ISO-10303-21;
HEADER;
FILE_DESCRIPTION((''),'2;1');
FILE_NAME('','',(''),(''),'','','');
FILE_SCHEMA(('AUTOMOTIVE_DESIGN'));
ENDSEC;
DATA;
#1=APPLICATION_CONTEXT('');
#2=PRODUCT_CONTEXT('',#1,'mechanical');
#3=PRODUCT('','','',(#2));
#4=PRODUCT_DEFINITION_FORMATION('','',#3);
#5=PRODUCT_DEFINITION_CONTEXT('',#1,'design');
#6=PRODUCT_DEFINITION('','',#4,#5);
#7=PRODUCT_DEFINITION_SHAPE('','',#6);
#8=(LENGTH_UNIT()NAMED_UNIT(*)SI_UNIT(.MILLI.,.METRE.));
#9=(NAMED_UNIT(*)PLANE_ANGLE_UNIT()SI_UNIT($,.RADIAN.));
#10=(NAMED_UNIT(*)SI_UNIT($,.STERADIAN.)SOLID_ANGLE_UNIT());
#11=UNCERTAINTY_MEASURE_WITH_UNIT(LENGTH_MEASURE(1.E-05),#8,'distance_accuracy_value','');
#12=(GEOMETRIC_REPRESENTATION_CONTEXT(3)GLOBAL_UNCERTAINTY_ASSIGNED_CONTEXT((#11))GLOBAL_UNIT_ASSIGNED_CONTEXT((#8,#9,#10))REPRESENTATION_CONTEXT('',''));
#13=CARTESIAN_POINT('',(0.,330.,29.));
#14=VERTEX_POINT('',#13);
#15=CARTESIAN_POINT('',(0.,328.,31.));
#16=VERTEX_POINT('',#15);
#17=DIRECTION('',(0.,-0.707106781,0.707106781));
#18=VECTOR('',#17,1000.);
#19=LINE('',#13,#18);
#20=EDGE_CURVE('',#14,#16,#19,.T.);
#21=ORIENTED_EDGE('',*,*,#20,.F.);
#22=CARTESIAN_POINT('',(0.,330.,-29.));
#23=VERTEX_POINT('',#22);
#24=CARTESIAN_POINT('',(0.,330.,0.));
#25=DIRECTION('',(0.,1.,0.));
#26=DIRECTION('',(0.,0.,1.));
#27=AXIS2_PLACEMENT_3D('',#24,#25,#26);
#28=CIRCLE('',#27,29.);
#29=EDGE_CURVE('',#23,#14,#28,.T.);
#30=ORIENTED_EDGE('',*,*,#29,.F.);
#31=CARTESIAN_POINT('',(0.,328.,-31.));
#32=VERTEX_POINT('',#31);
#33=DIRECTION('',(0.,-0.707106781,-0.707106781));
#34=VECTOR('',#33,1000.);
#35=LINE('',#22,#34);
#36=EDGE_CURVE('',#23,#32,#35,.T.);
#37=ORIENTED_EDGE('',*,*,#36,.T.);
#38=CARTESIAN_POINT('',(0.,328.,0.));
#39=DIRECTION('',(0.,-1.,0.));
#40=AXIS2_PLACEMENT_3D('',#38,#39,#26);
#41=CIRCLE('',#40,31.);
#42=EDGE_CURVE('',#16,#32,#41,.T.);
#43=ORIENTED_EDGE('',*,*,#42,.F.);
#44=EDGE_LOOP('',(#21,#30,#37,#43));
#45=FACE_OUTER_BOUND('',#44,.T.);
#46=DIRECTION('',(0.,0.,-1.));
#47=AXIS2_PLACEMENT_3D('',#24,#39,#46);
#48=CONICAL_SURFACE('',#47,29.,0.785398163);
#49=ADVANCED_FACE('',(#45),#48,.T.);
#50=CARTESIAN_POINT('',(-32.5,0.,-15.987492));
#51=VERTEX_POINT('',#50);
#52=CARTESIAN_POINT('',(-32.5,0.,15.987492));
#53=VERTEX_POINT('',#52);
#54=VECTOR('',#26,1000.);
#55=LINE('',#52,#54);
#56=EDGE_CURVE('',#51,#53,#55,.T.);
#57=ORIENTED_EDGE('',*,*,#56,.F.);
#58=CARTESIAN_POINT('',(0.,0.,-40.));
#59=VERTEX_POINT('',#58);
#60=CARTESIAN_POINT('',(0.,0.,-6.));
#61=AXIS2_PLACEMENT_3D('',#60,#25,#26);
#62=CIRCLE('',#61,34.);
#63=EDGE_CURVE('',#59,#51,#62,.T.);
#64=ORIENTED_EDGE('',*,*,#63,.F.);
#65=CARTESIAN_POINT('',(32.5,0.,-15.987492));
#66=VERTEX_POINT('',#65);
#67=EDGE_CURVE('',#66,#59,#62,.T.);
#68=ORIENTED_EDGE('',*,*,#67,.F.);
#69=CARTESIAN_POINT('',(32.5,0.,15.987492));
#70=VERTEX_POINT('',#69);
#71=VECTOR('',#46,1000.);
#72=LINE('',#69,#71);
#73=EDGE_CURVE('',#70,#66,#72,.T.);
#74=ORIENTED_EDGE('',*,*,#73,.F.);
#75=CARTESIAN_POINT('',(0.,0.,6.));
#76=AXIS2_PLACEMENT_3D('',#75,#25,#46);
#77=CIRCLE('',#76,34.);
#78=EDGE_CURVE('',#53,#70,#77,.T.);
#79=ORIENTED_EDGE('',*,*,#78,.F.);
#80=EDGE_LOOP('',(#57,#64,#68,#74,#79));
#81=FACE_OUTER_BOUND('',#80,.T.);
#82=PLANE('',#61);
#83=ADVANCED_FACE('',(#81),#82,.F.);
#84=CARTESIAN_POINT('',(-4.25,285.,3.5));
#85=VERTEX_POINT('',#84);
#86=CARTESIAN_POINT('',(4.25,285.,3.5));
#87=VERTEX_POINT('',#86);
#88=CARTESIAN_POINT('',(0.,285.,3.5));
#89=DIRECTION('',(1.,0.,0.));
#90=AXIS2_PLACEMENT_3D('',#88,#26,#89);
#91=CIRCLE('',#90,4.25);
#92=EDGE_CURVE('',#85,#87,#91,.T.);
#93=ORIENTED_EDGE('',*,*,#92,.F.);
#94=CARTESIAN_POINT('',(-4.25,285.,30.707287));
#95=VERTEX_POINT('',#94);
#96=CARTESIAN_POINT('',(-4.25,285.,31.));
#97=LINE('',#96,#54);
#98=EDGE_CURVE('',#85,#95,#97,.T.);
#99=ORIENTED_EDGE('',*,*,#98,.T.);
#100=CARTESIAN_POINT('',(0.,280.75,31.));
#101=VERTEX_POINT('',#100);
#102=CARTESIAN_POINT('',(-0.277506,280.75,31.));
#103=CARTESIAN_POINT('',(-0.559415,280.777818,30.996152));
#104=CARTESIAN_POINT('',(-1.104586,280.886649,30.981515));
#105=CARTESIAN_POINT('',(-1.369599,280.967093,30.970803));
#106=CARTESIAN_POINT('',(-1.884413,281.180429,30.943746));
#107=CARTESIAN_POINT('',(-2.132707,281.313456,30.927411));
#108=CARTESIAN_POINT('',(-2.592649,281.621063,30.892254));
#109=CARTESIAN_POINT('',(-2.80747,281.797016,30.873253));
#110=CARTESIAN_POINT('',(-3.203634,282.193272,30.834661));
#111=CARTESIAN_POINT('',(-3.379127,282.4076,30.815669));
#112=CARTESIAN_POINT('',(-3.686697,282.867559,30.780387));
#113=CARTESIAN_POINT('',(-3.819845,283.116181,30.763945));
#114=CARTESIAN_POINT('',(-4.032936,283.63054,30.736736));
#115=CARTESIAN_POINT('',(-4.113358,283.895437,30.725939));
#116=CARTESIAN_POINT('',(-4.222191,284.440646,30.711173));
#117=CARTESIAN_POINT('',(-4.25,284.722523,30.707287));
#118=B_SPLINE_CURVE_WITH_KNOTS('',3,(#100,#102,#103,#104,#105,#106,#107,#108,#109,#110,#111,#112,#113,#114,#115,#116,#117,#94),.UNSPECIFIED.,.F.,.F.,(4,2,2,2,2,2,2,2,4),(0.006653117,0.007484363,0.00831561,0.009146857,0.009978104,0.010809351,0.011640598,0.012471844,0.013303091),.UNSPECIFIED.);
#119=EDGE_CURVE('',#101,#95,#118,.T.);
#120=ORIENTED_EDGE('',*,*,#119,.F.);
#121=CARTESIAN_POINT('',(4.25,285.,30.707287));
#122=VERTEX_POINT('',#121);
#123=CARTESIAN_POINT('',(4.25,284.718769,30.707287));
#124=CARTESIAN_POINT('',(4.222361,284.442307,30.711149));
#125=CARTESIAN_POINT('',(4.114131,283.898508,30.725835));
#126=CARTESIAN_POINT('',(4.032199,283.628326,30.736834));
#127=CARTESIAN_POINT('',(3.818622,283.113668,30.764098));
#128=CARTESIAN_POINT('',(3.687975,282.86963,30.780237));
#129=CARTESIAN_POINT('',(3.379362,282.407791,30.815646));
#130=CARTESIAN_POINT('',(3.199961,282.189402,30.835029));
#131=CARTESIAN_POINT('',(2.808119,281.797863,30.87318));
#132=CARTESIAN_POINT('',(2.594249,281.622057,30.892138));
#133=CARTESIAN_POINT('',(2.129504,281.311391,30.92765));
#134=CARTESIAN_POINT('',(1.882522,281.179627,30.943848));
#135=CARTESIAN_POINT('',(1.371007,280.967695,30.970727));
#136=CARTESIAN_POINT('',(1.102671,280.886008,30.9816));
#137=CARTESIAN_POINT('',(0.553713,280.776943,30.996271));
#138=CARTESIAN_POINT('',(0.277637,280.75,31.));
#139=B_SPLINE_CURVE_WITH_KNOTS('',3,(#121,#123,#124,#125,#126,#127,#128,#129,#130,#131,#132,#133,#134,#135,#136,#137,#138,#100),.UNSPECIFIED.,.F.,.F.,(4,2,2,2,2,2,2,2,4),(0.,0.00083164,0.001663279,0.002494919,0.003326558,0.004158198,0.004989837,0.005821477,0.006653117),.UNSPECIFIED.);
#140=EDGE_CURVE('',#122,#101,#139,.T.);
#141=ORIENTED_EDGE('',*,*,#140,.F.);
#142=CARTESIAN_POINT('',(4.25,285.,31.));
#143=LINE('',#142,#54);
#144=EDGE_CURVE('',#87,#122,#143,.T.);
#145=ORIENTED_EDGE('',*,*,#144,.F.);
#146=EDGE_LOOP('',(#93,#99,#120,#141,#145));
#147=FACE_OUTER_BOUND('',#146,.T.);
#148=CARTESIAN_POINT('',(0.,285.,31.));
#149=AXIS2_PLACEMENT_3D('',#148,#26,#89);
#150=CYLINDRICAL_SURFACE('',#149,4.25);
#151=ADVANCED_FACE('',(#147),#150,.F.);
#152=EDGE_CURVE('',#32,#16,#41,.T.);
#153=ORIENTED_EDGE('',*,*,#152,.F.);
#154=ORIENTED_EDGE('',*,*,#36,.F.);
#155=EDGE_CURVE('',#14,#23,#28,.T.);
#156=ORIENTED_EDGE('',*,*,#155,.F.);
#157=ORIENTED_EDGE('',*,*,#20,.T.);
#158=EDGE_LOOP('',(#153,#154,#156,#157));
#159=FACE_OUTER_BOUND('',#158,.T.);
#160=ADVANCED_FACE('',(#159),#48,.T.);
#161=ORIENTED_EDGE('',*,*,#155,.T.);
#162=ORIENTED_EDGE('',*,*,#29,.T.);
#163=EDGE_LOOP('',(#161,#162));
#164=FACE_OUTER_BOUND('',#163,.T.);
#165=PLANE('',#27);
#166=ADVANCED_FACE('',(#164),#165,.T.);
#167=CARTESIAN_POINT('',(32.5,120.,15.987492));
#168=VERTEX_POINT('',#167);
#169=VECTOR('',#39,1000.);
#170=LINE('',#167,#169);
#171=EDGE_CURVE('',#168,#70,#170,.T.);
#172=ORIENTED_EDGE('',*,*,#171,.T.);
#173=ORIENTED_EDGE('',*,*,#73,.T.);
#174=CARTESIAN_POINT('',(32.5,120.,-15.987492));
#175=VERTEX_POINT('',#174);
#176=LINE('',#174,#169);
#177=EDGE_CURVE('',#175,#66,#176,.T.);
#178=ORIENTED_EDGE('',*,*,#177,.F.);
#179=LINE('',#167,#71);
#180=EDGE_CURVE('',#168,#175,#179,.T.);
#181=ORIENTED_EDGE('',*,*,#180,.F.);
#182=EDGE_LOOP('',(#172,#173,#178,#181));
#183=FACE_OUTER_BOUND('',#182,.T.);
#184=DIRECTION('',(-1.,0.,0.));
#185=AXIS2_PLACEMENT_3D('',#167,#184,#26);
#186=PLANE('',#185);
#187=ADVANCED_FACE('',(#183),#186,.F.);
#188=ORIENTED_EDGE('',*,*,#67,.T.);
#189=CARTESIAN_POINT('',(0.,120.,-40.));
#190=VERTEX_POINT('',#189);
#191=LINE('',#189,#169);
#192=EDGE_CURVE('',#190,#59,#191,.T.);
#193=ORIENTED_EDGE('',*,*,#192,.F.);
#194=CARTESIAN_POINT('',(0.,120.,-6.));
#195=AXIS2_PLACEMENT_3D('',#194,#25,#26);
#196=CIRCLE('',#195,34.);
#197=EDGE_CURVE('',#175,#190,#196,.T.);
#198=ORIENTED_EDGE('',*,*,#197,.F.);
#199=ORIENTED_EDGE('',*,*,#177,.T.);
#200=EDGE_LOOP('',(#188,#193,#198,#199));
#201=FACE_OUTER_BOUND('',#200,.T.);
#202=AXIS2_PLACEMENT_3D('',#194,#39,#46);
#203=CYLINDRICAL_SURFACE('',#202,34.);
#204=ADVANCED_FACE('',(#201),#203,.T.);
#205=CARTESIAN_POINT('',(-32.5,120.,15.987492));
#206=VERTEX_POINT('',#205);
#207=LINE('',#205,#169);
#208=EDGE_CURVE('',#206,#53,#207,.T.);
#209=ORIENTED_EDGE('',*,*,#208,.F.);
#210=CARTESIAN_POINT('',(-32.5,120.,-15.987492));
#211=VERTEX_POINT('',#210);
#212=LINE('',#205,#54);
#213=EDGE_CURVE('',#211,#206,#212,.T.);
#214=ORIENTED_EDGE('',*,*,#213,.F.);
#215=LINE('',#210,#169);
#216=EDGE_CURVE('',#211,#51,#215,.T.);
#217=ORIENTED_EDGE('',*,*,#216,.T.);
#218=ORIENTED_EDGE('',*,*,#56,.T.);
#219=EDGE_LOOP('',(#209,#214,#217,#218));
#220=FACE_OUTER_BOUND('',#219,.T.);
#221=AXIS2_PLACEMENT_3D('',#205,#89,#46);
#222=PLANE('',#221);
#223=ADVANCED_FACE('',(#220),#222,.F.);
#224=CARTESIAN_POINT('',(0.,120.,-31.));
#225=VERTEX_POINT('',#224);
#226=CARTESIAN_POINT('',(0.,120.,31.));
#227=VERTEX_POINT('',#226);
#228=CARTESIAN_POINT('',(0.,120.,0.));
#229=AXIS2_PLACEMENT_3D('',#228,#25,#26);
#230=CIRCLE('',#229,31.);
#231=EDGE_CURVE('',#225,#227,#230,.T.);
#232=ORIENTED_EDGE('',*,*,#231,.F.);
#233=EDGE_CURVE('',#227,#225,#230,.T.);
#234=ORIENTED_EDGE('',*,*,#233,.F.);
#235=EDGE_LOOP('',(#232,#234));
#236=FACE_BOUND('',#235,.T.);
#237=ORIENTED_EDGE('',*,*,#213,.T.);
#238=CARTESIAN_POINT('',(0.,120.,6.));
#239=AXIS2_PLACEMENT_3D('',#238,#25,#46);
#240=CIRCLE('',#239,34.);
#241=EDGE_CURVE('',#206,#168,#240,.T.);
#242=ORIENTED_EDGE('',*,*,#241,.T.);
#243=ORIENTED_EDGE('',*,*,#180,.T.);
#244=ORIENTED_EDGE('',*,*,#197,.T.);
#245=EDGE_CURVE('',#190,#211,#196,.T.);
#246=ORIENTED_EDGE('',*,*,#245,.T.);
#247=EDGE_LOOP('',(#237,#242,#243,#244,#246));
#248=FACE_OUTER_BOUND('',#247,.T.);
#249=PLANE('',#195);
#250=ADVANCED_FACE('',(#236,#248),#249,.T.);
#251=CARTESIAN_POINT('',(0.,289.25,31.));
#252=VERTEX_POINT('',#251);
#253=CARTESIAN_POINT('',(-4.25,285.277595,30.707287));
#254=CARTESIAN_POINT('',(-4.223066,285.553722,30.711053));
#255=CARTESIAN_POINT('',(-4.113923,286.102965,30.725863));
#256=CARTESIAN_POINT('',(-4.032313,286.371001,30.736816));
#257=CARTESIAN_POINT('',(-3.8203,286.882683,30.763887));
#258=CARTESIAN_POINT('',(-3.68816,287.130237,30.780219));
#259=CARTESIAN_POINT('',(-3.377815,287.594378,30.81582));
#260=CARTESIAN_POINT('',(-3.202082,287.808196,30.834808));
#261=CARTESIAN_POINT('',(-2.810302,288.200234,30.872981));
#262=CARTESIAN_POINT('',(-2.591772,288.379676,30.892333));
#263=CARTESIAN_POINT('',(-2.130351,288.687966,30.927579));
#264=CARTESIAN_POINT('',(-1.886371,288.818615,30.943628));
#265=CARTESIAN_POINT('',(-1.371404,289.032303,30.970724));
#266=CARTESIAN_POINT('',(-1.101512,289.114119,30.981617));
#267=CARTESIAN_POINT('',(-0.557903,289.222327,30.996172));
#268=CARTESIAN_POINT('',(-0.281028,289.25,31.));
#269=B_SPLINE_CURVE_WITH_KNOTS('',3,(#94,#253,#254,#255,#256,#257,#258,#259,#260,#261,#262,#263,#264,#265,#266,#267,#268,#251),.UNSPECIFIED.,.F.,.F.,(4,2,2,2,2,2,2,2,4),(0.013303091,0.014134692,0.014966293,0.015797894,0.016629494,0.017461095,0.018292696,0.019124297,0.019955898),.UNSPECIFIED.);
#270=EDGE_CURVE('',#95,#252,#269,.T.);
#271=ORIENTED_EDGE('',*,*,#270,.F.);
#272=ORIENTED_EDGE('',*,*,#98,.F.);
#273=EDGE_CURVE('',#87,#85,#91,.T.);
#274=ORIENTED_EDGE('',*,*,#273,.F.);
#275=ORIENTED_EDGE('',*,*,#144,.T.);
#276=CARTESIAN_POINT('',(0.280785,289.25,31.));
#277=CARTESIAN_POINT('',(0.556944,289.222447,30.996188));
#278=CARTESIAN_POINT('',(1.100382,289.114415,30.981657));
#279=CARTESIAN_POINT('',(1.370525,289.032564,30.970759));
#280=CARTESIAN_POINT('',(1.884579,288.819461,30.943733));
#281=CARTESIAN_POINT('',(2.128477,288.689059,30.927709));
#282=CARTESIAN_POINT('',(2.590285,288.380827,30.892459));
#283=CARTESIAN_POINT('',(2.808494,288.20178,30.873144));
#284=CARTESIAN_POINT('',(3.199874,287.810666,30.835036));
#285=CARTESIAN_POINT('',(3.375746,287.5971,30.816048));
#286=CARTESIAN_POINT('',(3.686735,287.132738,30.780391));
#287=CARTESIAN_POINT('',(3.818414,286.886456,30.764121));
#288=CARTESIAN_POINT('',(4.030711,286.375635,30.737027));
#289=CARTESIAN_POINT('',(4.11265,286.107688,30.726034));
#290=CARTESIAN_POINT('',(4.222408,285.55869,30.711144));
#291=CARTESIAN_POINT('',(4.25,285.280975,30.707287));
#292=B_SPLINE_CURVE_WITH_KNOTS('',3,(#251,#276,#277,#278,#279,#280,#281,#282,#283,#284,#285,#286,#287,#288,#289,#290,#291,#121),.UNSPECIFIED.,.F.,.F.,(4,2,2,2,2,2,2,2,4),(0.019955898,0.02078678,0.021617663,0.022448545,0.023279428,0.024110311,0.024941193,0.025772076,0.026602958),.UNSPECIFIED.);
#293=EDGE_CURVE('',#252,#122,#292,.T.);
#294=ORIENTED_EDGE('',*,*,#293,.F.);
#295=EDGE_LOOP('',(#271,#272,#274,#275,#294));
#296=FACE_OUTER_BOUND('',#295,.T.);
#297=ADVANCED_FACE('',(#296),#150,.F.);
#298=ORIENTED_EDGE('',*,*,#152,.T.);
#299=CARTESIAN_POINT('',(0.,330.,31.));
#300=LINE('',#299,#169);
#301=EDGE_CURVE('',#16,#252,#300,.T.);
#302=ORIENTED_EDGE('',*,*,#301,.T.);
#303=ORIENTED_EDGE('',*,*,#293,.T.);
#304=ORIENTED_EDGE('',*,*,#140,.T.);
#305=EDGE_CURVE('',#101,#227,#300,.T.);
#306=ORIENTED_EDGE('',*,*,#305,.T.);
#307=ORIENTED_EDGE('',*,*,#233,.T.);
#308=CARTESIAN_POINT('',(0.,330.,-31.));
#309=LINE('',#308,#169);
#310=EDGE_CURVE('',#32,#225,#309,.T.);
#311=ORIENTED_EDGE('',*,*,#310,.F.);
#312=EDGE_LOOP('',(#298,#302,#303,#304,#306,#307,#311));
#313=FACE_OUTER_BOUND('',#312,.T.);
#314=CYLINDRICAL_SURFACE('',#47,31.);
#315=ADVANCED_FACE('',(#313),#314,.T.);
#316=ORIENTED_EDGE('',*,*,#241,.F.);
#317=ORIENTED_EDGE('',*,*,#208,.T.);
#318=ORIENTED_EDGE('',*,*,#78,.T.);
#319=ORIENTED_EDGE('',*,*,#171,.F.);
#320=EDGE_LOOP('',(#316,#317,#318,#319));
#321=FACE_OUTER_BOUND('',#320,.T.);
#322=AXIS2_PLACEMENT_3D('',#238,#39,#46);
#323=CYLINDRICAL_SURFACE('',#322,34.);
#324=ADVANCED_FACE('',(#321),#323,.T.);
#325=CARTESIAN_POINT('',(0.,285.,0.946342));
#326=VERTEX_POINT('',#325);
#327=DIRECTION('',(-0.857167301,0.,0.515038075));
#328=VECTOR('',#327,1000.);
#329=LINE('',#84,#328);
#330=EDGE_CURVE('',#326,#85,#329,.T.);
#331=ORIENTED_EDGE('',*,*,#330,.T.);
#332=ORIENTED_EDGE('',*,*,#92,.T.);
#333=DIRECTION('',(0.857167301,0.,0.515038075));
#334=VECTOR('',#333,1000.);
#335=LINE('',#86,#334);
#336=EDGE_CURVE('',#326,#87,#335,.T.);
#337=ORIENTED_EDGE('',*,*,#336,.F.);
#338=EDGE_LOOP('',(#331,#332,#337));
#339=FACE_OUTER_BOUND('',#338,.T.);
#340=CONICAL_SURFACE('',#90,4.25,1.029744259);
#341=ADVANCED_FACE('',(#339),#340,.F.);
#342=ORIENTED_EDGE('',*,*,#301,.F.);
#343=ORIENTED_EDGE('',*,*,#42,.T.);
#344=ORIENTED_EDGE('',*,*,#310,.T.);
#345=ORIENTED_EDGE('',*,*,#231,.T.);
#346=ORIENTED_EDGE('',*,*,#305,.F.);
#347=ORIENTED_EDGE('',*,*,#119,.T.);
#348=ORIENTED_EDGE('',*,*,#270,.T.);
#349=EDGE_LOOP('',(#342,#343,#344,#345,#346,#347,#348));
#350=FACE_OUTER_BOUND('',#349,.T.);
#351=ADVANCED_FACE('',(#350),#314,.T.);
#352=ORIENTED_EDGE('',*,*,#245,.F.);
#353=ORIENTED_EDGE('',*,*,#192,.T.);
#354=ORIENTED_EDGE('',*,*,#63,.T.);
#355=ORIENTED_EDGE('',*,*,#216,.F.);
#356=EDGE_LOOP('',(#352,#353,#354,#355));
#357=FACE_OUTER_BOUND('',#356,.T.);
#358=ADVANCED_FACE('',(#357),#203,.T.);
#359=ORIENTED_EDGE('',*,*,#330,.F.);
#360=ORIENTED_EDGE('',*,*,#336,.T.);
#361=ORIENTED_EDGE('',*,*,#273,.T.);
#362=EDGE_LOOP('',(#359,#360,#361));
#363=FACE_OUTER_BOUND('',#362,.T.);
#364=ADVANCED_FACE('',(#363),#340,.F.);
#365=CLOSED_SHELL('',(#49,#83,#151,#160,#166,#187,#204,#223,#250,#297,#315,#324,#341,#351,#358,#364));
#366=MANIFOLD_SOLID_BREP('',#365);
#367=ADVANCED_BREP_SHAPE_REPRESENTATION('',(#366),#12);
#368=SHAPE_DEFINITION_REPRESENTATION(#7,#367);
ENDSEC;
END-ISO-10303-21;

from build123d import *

# Parameters (mm, degrees)
EXTRUDE_1_DEPTH         = 120
SKETCH_2_R              = 31
EXTRUDE_2_DEPTH         = 210
HOLE_WIZARD_M10_1_D     = 8.5
HOLE_WIZARD_M10_1_DEPTH = 27.5
HOLE_WIZARD_M10_1_TIP   = 2.553657631
CHAMFER_1_SIZE          = 2


with BuildPart() as part:
    # 草图1 → 凸台-拉伸1 (new body)
    with BuildSketch(Plane(origin=(0, 0, 0), x_dir=(1, 0, 0), z_dir=(0, 1, 0))):
        with BuildLine():
            Line((32.5, -15.987492178), (32.5, 15.987492178))
            ThreePointArc((32.5, 15.987492178), (0, 40), (-32.5, 15.987492178))
            Line((-32.5, 15.987492178), (-32.5, -15.987492178))
            ThreePointArc((-32.5, -15.987492178), (0, -40), (32.5, -15.987492178))
        make_face()
    extrude(amount=EXTRUDE_1_DEPTH)

    # 草图2 → 凸台-拉伸2 (add)
    with BuildSketch(Plane(origin=(0, 120, 0), x_dir=(1, 0, 0), z_dir=(0, 1, 0))):
        with Locations(Location((0, 0, 0), (0, 0, 270))):
            Circle(SKETCH_2_R)
    extrude(amount=EXTRUDE_2_DEPTH)

    # M10 螺纹孔1
    with Locations(Plane.XY.offset(31)):
        with Locations((0, 285)):
            Hole(HOLE_WIZARD_M10_1_D / 2, depth=HOLE_WIZARD_M10_1_DEPTH)
            with Locations((0, 0, -(HOLE_WIZARD_M10_1_DEPTH + HOLE_WIZARD_M10_1_TIP / 2))):  # 118° drill point
                Cone(0, HOLE_WIZARD_M10_1_D / 2, HOLE_WIZARD_M10_1_TIP, mode=Mode.SUBTRACT)

    # 倒角1
    chamfer_1_edges = [part.edges().sort_by_distance(p)[0] for p in [
        (0, 330, -31),
    ]]
    chamfer(chamfer_1_edges, length=CHAMFER_1_SIZE)


solid = part.part
